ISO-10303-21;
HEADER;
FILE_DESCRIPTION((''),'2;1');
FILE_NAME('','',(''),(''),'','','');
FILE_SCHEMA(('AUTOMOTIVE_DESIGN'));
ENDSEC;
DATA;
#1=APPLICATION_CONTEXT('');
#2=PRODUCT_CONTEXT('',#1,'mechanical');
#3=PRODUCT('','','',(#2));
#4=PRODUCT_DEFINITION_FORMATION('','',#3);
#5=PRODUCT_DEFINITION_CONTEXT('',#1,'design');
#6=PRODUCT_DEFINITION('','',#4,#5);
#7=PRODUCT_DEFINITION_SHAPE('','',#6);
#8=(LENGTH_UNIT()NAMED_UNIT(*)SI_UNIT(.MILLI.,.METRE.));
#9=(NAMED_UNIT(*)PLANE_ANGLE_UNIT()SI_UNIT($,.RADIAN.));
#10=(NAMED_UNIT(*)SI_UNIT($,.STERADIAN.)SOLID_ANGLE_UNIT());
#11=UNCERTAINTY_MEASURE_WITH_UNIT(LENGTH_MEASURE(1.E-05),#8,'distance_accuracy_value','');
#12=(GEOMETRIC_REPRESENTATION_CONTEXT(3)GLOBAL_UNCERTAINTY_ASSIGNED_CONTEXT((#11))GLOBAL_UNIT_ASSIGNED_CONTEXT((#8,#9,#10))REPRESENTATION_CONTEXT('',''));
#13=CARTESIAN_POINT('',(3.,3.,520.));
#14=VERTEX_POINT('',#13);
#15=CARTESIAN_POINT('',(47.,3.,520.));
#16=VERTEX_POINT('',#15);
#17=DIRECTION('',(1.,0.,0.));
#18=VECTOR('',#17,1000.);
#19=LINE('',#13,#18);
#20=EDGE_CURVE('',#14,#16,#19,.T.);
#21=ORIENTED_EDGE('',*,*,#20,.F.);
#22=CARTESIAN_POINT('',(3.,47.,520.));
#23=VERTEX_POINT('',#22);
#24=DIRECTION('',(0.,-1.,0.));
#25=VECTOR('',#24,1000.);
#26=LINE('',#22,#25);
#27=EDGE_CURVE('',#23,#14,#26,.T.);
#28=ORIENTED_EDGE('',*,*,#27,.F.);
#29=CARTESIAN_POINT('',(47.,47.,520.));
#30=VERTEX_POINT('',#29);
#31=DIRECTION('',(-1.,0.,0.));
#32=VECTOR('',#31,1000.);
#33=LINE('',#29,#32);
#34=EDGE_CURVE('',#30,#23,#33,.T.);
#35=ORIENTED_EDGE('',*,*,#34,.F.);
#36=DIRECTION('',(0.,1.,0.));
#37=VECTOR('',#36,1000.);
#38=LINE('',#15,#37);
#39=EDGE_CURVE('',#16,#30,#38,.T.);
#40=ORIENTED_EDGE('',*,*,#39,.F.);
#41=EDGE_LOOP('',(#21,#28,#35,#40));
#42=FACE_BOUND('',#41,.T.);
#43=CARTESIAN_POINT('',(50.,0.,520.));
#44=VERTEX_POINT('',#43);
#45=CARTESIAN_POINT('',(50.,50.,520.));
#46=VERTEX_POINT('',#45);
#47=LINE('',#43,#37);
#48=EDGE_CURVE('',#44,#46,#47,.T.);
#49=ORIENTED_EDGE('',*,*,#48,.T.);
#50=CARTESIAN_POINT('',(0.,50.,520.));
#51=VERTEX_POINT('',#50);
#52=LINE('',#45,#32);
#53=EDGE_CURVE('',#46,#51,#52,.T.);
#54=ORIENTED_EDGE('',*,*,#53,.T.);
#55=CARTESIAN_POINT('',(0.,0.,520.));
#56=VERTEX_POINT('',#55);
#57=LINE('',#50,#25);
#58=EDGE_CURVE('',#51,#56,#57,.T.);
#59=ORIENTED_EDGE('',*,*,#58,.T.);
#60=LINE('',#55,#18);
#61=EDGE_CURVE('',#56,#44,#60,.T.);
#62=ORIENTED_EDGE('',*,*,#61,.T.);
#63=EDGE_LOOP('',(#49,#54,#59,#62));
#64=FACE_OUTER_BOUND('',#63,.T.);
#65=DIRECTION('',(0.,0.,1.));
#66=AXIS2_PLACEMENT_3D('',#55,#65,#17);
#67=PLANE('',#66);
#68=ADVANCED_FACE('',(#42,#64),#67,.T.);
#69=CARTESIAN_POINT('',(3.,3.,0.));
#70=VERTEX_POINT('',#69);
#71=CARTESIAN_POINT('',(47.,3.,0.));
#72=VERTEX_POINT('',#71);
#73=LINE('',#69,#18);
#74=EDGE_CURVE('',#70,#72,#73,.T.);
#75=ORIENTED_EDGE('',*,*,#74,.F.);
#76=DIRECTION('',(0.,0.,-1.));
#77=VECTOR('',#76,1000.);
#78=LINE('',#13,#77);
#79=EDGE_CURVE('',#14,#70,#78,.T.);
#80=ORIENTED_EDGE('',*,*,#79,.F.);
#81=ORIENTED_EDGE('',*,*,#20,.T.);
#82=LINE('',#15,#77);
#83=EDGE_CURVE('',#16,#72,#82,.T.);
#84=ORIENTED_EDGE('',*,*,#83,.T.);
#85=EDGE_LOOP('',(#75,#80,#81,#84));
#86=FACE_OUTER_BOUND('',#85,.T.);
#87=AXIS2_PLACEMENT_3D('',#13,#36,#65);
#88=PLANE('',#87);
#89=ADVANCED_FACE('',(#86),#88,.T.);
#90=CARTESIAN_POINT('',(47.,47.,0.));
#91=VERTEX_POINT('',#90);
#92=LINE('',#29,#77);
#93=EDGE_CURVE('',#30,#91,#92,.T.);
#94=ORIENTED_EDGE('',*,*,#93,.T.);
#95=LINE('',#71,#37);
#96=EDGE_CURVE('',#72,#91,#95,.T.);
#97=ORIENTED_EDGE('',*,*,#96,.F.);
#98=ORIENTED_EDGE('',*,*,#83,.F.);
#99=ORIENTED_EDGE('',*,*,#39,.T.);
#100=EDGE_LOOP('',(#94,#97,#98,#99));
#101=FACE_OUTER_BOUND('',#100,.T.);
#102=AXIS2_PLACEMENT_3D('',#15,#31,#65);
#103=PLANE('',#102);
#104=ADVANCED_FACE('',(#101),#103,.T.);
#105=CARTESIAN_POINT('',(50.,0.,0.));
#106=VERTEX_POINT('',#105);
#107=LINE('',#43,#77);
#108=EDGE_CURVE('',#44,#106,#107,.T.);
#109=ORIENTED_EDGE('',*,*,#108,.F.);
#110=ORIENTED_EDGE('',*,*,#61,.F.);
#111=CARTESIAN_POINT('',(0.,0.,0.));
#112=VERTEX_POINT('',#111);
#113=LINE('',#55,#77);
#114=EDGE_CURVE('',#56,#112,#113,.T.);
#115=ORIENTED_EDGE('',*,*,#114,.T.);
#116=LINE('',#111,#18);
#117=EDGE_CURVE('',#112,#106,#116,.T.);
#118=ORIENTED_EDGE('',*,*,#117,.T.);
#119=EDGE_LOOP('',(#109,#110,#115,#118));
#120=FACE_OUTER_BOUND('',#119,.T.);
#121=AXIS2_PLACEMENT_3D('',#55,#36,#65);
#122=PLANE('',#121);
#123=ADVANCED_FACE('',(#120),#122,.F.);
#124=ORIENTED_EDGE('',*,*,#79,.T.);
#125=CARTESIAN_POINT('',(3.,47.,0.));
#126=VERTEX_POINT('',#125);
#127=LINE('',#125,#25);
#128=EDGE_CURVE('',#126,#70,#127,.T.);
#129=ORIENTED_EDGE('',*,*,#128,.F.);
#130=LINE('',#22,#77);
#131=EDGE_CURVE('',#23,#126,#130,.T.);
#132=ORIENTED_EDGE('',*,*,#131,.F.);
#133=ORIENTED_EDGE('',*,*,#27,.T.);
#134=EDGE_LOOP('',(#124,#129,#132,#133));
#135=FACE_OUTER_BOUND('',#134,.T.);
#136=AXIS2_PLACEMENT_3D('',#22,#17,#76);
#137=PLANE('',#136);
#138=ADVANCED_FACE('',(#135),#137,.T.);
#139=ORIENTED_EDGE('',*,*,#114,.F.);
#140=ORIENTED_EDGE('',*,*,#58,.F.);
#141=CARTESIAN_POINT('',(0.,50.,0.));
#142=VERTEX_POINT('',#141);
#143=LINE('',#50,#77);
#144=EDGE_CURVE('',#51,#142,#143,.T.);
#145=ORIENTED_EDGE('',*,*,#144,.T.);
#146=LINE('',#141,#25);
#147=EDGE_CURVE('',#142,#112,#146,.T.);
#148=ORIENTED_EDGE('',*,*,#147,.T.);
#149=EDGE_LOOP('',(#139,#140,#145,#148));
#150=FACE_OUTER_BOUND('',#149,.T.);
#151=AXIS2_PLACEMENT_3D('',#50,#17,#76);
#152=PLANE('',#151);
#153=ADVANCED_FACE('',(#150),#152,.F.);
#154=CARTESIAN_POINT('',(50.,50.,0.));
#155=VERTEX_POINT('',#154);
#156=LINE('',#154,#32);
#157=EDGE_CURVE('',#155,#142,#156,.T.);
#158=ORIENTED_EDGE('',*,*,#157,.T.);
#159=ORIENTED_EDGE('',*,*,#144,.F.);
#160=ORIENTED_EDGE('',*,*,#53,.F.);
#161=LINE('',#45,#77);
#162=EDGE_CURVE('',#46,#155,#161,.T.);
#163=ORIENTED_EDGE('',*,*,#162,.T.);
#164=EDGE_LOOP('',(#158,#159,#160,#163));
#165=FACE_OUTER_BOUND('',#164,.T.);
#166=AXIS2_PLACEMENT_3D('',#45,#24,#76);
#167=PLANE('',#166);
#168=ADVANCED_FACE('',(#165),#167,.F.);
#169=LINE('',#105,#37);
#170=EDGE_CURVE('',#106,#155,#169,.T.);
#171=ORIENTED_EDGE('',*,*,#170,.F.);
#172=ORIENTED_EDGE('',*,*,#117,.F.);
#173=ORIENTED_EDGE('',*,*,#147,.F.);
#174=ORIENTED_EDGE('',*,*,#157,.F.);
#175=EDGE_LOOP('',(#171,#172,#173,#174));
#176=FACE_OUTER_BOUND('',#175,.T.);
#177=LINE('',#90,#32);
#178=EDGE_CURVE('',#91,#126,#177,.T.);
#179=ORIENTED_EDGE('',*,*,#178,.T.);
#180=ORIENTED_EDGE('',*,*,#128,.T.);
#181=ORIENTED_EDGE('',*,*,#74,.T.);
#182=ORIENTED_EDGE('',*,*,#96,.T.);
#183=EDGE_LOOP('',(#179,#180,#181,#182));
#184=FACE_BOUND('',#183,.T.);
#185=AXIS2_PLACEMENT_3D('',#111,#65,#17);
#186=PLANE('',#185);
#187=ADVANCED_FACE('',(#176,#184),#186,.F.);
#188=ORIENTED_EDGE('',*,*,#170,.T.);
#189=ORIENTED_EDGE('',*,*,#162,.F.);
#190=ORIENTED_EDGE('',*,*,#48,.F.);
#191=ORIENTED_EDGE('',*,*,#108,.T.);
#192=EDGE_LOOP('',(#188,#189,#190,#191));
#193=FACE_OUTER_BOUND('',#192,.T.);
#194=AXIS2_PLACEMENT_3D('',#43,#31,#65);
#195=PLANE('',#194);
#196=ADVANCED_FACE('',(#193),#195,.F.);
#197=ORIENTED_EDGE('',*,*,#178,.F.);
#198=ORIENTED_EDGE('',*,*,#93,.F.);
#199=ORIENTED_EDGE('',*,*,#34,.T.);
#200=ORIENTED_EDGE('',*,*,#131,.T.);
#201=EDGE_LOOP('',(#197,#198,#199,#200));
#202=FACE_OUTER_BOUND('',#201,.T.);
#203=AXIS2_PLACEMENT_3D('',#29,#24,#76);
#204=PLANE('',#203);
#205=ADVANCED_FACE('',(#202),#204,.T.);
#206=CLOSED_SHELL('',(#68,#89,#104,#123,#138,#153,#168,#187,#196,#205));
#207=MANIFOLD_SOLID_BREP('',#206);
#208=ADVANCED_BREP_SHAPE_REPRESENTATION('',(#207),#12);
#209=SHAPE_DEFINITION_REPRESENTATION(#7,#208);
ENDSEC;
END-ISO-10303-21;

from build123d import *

# Parameters (mm, degrees)
SKETCH_1_W          = 50
SKETCH_1_H          = 50
SKETCH_1_W_2        = 44
SKETCH_1_H_2        = 44
EXTRUDE_1_DEPTH     = 520
SKETCH_2_W          = 50
SKETCH_2_H          = 50
SKETCH_2_W_2        = 44
SKETCH_2_H_2        = 44
EXTRUDE_2_DEPTH     = 70
SKETCH_3_W          = 50
SKETCH_3_H          = 50
CUT_EXTRUDE_1_DEPTH = 70


with BuildPart() as part:
    # 草图1 → 凸台-拉伸1 (new body)
    with BuildSketch(Plane.XY):
        with Locations((25, 25)):
            Rectangle(SKETCH_1_W, SKETCH_1_H)
        with Locations((25, 25)):
            Rectangle(SKETCH_1_W_2, SKETCH_1_H_2, mode=Mode.SUBTRACT)
    extrude(amount=EXTRUDE_1_DEPTH)

    # 草图2 → 凸台-拉伸2 (add)
    with BuildSketch(Plane.XY.offset(520)):
        with Locations((25, 25)):
            Rectangle(SKETCH_2_W, SKETCH_2_H)
        with Locations((25, 25)):
            Rectangle(SKETCH_2_W_2, SKETCH_2_H_2, mode=Mode.SUBTRACT)
    extrude(amount=EXTRUDE_2_DEPTH)

    # 草图3 → 切除-拉伸1 (cut)
    with BuildSketch(Plane.XY.offset(590)):
        with Locations((25, 25)):
            Rectangle(SKETCH_3_W, SKETCH_3_H)
    extrude(amount=-CUT_EXTRUDE_1_DEPTH, mode=Mode.SUBTRACT)


solid = part.part
